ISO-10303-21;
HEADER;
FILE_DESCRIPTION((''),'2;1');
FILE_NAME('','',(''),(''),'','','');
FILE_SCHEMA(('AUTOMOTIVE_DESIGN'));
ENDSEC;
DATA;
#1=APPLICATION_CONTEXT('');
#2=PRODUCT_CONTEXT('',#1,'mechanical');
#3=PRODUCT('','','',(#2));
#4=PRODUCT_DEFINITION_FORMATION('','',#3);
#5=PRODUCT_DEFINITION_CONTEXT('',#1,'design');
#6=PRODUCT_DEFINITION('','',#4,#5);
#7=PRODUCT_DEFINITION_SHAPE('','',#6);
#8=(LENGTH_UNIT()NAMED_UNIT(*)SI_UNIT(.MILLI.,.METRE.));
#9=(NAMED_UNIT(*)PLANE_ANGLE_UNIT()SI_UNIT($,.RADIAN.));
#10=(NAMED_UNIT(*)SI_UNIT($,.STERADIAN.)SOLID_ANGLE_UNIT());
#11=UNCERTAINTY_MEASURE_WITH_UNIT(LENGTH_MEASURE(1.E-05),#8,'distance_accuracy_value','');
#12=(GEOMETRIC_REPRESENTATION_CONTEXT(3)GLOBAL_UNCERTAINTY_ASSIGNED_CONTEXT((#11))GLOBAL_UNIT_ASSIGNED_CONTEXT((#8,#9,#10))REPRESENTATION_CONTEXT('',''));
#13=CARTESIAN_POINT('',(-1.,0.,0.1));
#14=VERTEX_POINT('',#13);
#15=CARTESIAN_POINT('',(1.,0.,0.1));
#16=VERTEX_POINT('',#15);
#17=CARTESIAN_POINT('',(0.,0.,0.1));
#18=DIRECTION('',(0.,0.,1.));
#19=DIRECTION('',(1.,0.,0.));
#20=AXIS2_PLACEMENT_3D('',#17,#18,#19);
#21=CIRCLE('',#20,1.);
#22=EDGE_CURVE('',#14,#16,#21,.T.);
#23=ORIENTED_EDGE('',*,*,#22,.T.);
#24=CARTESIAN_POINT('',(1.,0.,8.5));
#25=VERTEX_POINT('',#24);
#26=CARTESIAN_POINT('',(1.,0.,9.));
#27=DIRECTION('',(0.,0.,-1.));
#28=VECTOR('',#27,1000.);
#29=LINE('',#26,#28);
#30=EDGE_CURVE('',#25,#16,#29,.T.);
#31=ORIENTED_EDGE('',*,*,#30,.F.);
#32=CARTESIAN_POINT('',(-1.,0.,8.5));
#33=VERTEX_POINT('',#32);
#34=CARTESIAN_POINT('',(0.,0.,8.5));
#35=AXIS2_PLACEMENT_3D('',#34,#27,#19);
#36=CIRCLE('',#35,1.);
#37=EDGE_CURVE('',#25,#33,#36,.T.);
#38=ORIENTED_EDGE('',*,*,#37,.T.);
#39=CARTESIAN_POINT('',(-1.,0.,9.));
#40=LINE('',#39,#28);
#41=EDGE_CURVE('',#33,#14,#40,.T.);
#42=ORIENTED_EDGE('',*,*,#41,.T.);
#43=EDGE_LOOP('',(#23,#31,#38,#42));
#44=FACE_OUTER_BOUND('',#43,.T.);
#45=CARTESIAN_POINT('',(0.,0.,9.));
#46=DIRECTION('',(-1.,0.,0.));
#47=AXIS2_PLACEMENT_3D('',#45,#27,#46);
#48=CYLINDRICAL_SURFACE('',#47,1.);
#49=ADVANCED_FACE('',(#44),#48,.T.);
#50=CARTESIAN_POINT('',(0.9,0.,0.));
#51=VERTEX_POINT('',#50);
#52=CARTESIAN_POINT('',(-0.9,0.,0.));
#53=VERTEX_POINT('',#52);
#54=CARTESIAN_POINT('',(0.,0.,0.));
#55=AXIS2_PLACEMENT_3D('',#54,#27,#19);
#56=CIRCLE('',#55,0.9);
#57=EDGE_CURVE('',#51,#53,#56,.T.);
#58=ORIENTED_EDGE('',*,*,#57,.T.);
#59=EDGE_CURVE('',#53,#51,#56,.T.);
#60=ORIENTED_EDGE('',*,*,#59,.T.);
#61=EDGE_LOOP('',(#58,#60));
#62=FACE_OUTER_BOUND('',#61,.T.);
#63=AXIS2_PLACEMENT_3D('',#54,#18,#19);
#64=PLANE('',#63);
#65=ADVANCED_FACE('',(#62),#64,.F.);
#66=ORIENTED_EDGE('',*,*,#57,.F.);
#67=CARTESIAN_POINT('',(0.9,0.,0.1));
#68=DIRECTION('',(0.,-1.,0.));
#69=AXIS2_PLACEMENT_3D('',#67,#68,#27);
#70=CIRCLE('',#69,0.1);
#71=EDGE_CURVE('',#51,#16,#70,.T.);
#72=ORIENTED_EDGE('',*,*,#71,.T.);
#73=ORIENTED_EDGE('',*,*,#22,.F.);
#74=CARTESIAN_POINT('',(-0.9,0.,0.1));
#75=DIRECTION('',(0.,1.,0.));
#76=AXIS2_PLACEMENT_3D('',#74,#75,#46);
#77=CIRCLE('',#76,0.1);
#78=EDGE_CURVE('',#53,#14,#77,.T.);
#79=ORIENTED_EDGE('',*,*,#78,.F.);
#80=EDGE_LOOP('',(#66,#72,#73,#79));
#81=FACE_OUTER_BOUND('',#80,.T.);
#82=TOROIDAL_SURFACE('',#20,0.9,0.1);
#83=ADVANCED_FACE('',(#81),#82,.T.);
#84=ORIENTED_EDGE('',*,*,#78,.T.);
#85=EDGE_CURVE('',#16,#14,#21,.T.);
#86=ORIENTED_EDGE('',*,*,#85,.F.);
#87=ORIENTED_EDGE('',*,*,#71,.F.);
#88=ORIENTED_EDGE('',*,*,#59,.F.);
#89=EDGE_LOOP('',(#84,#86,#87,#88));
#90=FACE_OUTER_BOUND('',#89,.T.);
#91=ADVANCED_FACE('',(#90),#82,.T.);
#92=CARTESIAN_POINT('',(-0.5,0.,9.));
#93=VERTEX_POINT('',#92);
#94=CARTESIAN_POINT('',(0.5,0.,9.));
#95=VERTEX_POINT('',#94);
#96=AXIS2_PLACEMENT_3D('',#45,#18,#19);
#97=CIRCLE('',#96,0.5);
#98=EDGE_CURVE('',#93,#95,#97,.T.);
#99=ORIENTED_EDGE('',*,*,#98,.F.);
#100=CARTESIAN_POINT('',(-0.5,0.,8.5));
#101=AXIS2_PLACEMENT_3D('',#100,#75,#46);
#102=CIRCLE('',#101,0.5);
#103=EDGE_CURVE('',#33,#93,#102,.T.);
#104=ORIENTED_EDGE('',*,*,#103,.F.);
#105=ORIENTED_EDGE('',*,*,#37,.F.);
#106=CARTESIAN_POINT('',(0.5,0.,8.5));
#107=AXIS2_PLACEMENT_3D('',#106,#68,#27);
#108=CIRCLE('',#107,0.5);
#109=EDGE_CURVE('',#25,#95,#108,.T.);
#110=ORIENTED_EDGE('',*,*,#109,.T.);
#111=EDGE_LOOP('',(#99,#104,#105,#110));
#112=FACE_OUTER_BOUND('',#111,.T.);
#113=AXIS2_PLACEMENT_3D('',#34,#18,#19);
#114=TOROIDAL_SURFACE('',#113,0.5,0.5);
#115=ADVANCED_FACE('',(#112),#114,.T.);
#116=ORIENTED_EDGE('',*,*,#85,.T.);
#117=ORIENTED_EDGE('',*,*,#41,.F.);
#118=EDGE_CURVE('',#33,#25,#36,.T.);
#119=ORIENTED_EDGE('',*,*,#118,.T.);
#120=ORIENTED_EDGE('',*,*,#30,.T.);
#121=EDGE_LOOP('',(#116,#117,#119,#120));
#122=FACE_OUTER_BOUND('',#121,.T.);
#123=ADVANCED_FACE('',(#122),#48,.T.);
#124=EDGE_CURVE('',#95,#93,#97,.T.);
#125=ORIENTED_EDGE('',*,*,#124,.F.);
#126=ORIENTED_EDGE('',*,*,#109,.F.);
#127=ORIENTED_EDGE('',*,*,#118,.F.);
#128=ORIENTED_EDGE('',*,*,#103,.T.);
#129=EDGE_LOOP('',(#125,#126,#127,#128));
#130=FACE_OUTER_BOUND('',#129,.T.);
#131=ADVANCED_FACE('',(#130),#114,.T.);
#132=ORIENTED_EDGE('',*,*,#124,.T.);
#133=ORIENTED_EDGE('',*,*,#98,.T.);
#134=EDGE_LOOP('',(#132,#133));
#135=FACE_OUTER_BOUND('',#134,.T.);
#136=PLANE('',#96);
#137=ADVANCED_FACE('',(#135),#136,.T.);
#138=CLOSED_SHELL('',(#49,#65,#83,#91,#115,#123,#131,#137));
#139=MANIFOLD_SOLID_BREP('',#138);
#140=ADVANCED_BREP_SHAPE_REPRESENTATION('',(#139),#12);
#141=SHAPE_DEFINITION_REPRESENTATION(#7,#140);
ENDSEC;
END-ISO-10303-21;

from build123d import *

# Parameters (mm, degrees)
SKETCH1_R           = 1
BOSS_EXTRUDE1_DEPTH = 9
FILLET1_R           = 0.5
FILLET2_R           = 0.1


with BuildPart() as part:
    # Sketch1 → Boss-Extrude1 (new body)
    with BuildSketch(Plane.XY):
        Circle(SKETCH1_R)
    extrude(amount=BOSS_EXTRUDE1_DEPTH)

    # Fillet1
    fillet1_edges = [part.edges().sort_by_distance(p)[0] for p in [
        (-1, 0, 9),
    ]]
    fillet(fillet1_edges, radius=FILLET1_R)

    # Fillet2
    fillet2_edges = [part.edges().sort_by_distance(p)[0] for p in [
        (-1, 0, 0),
    ]]
    fillet(fillet2_edges, radius=FILLET2_R)


solid = part.part
